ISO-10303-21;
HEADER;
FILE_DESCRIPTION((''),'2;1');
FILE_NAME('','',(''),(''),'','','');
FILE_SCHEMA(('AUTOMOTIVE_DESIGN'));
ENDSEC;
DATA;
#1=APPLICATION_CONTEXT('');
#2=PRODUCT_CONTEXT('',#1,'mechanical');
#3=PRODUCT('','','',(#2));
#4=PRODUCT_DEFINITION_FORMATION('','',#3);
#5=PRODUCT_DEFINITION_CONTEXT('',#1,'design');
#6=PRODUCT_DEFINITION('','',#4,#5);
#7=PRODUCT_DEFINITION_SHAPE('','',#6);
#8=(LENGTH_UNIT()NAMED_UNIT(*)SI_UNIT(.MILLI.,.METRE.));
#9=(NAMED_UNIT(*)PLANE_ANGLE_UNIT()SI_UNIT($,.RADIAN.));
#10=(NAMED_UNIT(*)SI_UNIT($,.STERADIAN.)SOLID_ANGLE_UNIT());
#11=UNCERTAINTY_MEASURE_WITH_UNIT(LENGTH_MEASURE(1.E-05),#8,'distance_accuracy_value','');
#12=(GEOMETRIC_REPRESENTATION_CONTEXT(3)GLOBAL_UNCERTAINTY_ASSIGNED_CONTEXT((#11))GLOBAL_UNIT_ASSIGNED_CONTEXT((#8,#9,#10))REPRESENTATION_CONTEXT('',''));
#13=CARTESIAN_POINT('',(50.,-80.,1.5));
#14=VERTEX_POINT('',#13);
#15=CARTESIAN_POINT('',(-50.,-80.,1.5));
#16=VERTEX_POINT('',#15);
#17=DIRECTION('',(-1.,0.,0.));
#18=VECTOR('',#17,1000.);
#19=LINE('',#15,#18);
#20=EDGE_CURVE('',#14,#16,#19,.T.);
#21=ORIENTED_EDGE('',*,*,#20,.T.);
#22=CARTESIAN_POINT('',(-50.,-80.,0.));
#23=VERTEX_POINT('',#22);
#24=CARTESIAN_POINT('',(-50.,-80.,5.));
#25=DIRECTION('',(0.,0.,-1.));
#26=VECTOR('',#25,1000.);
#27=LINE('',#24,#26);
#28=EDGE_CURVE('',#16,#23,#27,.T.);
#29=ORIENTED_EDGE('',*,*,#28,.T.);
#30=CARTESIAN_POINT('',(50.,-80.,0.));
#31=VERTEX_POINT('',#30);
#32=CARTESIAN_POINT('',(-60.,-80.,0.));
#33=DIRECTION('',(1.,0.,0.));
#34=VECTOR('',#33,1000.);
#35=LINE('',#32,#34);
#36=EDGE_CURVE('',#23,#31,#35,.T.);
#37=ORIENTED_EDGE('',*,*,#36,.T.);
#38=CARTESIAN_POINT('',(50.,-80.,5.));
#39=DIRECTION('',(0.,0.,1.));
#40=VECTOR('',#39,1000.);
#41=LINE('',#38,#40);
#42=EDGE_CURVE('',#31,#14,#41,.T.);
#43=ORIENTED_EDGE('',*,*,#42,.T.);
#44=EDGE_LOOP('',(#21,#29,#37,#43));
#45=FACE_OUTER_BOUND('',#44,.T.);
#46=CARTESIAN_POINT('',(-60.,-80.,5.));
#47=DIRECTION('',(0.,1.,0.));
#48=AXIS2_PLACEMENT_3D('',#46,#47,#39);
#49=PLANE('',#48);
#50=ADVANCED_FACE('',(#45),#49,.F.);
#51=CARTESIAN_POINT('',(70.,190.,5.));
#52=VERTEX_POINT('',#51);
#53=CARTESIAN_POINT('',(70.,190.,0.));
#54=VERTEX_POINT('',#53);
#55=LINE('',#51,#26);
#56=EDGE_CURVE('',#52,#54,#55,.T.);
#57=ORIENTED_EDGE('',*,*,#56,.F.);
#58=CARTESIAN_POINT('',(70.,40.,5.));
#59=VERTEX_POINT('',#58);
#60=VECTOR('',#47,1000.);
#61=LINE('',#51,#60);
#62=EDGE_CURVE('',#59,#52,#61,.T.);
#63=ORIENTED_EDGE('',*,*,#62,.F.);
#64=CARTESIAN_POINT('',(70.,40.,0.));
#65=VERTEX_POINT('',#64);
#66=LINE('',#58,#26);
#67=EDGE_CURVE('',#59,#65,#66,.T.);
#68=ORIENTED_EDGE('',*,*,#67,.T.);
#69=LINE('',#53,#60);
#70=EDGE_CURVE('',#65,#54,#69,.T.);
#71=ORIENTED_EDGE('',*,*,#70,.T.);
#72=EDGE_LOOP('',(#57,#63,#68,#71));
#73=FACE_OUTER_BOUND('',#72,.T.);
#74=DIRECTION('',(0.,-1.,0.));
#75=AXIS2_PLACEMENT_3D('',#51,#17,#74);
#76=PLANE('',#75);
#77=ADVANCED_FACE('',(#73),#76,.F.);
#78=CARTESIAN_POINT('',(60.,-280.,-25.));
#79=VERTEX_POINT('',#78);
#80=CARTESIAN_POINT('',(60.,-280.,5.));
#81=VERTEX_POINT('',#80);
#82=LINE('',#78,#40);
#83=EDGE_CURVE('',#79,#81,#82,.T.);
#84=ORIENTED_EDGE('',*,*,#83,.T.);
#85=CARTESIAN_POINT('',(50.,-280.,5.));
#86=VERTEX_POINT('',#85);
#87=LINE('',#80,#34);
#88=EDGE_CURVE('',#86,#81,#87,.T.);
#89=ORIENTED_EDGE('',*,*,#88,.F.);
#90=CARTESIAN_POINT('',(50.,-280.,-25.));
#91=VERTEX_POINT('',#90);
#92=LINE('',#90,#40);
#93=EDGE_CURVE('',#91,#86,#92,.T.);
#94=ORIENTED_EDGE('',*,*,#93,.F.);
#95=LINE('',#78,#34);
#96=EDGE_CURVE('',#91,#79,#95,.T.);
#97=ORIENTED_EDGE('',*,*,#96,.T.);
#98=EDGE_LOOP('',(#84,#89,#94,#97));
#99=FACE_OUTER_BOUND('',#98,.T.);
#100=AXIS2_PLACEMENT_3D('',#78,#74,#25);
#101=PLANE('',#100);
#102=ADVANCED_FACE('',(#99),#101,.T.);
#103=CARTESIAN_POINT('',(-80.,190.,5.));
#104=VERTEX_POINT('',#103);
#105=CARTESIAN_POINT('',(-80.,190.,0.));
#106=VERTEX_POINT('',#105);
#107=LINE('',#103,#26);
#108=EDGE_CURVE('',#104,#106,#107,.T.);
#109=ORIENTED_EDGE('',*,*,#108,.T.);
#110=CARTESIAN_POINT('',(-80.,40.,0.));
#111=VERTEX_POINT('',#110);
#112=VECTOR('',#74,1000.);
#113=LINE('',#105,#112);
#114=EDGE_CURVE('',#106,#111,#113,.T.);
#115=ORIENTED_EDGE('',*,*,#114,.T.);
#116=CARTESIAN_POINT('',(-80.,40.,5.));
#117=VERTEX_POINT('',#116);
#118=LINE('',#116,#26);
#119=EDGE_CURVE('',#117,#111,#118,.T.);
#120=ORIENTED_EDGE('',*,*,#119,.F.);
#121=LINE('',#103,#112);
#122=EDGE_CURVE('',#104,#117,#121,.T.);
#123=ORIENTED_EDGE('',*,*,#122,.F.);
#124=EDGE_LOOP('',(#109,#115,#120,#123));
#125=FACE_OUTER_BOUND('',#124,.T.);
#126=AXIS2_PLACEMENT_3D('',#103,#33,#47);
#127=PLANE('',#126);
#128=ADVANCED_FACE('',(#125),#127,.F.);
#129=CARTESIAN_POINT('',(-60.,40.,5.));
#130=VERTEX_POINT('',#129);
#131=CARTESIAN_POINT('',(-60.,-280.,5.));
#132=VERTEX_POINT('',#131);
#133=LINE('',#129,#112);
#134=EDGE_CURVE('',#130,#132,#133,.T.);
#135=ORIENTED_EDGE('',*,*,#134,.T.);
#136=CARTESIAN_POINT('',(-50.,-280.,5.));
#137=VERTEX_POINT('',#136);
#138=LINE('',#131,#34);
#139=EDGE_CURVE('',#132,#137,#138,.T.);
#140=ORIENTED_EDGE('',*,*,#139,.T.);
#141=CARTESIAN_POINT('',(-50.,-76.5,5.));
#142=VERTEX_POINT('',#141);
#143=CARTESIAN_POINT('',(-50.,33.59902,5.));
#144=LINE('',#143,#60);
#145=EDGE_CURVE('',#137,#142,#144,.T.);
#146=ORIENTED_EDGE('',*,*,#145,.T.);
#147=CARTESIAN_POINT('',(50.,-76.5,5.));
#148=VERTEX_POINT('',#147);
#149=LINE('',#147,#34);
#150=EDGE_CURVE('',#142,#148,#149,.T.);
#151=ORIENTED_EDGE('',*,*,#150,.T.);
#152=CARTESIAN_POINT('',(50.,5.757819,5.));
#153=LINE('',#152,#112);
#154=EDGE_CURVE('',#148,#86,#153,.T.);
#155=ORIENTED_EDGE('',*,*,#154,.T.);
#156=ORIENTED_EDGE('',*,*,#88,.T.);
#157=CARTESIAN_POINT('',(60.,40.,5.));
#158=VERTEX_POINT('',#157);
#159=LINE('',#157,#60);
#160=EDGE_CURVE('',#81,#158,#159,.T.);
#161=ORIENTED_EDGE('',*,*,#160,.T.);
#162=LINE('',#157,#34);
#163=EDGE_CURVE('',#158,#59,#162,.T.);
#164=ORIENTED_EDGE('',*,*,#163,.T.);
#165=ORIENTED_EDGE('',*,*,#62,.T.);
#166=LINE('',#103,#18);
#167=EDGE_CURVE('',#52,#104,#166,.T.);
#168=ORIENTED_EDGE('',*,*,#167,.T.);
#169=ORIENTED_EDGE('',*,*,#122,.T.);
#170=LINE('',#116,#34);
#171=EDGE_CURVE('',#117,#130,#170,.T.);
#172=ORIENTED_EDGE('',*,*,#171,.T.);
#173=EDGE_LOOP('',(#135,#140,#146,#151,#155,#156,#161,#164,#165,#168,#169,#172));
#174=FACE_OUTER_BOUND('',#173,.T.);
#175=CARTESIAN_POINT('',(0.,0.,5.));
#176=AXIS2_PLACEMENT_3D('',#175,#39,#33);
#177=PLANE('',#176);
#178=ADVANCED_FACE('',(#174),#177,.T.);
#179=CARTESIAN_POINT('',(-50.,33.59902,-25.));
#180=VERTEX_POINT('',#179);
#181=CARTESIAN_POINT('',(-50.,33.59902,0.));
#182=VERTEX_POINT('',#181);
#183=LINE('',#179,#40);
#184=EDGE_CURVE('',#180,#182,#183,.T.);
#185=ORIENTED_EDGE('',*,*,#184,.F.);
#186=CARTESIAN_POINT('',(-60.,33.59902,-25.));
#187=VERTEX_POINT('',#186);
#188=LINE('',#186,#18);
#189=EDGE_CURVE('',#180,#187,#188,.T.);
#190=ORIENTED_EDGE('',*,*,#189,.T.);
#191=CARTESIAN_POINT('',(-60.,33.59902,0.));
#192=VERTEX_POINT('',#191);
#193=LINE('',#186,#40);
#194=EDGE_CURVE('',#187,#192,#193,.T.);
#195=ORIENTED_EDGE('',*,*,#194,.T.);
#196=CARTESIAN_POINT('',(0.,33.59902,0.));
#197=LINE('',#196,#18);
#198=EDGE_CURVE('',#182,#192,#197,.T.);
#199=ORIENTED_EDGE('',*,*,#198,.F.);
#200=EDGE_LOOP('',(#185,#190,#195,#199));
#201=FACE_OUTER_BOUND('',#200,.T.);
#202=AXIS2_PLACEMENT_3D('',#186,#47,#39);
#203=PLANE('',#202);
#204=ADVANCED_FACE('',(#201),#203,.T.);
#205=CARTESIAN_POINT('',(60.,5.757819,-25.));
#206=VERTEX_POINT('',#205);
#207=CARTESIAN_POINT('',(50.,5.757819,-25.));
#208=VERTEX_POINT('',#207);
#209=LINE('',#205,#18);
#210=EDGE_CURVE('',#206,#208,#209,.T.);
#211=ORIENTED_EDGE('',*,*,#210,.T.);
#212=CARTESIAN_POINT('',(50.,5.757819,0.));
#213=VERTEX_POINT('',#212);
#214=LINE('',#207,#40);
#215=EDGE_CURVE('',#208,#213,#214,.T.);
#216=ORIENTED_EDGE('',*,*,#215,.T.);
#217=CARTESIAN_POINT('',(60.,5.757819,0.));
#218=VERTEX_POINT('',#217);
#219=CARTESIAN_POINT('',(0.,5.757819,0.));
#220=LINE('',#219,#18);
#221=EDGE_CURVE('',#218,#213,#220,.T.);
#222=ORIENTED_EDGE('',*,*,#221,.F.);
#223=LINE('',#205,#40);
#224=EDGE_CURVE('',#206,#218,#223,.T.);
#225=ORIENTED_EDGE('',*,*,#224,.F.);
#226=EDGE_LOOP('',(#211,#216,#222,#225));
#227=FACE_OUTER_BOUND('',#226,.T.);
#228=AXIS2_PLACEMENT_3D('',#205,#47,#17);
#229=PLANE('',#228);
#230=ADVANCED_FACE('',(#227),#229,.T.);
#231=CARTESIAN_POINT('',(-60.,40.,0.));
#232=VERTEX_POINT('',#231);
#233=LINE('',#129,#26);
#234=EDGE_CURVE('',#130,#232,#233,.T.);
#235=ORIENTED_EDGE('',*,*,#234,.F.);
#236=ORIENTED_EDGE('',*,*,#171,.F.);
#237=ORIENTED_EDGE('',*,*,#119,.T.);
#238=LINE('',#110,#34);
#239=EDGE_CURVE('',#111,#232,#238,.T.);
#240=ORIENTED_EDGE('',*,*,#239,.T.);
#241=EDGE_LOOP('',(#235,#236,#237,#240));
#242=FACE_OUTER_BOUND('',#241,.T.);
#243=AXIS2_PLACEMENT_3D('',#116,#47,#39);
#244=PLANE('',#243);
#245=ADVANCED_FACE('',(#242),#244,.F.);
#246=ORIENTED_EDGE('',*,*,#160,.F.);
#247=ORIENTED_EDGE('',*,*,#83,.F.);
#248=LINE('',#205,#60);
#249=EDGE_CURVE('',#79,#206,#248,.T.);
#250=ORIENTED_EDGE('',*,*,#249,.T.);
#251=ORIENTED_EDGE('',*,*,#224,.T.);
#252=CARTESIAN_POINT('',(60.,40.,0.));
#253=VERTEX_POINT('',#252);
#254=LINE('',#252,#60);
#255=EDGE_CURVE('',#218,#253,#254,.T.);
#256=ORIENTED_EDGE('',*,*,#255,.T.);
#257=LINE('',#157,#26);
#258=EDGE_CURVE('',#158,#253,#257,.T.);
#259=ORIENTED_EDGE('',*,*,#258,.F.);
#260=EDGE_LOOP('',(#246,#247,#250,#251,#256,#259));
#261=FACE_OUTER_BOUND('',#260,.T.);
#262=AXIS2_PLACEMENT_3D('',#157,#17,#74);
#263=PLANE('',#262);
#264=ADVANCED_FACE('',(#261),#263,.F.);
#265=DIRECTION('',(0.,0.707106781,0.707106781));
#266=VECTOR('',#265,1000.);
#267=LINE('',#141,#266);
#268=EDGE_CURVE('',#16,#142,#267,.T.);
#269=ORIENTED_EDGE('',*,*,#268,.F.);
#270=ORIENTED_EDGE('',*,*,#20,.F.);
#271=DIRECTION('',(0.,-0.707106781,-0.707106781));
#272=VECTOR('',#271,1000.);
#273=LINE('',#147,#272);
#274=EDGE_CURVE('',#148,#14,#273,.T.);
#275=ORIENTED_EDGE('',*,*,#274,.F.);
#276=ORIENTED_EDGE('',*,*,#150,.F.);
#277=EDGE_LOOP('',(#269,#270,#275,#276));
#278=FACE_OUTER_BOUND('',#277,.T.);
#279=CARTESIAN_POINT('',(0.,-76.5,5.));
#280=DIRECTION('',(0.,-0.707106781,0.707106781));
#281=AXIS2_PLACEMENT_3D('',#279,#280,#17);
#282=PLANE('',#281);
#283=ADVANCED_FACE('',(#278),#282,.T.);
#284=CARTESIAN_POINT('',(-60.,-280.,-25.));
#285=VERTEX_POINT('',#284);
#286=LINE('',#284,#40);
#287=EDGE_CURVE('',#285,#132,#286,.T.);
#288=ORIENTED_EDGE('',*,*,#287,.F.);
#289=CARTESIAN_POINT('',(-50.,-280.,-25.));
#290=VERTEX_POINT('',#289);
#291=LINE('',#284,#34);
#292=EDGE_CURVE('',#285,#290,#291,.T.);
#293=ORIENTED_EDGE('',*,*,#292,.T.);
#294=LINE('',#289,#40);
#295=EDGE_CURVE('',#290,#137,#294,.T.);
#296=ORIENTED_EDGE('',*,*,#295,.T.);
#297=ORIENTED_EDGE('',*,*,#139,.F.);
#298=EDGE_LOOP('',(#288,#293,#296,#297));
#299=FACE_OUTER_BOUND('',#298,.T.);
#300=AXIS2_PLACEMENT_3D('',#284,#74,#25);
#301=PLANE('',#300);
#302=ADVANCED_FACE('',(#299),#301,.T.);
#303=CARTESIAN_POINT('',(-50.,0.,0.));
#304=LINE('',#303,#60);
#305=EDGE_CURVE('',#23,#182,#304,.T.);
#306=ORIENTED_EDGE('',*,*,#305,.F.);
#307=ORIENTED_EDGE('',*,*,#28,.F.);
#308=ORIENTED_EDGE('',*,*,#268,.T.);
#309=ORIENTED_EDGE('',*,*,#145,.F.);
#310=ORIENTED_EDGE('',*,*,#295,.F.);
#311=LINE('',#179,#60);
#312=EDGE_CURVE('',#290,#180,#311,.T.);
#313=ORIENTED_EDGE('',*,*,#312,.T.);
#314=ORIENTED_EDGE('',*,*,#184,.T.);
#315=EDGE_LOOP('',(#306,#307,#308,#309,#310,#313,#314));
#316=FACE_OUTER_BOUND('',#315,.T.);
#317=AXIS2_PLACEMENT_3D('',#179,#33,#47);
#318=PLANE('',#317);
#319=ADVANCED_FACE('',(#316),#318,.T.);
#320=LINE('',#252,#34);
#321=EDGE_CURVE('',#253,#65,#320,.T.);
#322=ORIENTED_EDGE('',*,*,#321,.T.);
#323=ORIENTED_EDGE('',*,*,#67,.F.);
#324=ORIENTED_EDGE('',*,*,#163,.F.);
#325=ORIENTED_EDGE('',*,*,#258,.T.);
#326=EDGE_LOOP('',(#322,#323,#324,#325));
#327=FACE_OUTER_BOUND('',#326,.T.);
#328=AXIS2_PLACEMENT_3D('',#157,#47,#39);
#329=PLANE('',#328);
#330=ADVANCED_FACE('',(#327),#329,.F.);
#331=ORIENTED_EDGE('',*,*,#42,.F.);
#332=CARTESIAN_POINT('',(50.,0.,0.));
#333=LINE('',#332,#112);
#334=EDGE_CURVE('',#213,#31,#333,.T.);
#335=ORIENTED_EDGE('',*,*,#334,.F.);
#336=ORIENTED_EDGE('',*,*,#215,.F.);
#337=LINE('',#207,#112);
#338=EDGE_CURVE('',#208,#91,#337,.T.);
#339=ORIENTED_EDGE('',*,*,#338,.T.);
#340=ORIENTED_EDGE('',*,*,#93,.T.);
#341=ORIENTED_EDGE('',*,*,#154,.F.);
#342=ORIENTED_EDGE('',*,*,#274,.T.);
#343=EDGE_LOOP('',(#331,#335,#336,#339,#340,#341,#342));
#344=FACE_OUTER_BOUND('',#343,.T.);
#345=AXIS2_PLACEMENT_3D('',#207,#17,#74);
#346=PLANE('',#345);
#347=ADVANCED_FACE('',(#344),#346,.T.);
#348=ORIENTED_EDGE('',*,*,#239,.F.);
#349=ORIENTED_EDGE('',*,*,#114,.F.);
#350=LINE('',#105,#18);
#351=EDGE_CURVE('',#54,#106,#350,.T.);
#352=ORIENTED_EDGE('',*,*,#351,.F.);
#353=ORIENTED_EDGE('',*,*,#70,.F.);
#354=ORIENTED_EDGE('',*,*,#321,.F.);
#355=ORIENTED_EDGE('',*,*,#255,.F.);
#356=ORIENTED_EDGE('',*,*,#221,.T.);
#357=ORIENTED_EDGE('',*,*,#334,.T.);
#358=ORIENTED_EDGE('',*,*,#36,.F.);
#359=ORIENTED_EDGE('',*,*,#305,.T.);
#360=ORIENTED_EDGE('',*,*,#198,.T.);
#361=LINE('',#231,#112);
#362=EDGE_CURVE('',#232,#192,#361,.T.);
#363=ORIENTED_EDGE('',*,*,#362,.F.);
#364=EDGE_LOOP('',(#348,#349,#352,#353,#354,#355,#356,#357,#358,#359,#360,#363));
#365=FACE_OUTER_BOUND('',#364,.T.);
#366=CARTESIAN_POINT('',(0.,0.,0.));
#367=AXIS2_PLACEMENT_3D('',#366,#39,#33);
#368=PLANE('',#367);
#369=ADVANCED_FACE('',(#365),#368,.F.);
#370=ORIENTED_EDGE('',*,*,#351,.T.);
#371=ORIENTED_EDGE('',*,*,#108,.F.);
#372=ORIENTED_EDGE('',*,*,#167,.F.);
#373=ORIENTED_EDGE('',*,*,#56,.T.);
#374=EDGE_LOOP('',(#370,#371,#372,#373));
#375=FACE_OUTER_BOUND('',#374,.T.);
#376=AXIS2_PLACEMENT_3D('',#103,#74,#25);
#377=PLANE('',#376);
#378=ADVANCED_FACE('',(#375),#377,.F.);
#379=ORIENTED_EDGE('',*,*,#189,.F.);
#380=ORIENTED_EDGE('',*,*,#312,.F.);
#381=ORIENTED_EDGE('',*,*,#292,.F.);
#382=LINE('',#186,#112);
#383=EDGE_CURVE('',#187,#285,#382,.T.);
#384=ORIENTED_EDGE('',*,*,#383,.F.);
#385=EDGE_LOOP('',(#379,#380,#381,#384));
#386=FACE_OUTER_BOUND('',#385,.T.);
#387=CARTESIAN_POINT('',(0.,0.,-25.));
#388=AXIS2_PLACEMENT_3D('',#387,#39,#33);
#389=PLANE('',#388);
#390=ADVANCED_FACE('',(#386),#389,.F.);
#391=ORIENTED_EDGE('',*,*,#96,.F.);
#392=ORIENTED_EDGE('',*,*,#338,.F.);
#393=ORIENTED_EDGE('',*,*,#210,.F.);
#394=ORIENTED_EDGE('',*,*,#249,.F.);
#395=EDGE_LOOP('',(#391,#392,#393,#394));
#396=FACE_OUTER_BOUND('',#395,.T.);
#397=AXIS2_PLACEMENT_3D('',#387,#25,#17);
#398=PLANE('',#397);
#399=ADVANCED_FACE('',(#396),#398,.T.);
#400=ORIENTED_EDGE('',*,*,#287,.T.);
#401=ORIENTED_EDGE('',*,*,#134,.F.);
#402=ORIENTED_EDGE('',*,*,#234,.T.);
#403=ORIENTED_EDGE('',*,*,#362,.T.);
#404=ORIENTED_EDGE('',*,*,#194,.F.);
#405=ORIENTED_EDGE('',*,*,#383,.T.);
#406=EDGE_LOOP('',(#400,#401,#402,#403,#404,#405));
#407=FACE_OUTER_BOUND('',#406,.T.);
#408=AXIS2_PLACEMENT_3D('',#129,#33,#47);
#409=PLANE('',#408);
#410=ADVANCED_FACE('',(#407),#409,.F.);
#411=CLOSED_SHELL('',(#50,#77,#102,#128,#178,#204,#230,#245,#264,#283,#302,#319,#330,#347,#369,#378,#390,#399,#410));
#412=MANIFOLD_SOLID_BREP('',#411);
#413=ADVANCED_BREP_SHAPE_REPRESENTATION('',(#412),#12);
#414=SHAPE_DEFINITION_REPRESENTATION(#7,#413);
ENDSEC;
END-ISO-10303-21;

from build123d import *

# Parameters (mm, degrees)
BOSS_EXTRUDE1_DEPTH = 5
SKETCH2_W           = 10
SKETCH2_H           = 285.757818937
SKETCH2_H_2         = 313.599020197
BOSS_EXTRUDE2_DEPTH = 30
CHAMFER1_SIZE       = 3.5


with BuildPart() as part:
    # Sketch1 → Boss-Extrude1 (new body)
    with BuildSketch(Plane.XY):
        Polygon((-60, 40), (-60, -80), (60, -80), (60, 40), (70, 40), (70, 190), (-80, 190), (-80, 40), align=None)
    extrude(amount=BOSS_EXTRUDE1_DEPTH)

    # Sketch2 → Boss-Extrude2 (add)
    with BuildSketch(Plane.XY.offset(5)):
        with Locations((55, -137.121090531)):
            Rectangle(SKETCH2_W, SKETCH2_H)
        with Locations((-55, -123.200489901)):
            Rectangle(SKETCH2_W, SKETCH2_H_2)
    extrude(amount=-BOSS_EXTRUDE2_DEPTH)

    # Chamfer1
    chamfer1_edges = [part.edges().sort_by_distance(p)[0] for p in [
        (0, -80, 5),
    ]]
    chamfer(chamfer1_edges, length=CHAMFER1_SIZE)


solid = part.part
